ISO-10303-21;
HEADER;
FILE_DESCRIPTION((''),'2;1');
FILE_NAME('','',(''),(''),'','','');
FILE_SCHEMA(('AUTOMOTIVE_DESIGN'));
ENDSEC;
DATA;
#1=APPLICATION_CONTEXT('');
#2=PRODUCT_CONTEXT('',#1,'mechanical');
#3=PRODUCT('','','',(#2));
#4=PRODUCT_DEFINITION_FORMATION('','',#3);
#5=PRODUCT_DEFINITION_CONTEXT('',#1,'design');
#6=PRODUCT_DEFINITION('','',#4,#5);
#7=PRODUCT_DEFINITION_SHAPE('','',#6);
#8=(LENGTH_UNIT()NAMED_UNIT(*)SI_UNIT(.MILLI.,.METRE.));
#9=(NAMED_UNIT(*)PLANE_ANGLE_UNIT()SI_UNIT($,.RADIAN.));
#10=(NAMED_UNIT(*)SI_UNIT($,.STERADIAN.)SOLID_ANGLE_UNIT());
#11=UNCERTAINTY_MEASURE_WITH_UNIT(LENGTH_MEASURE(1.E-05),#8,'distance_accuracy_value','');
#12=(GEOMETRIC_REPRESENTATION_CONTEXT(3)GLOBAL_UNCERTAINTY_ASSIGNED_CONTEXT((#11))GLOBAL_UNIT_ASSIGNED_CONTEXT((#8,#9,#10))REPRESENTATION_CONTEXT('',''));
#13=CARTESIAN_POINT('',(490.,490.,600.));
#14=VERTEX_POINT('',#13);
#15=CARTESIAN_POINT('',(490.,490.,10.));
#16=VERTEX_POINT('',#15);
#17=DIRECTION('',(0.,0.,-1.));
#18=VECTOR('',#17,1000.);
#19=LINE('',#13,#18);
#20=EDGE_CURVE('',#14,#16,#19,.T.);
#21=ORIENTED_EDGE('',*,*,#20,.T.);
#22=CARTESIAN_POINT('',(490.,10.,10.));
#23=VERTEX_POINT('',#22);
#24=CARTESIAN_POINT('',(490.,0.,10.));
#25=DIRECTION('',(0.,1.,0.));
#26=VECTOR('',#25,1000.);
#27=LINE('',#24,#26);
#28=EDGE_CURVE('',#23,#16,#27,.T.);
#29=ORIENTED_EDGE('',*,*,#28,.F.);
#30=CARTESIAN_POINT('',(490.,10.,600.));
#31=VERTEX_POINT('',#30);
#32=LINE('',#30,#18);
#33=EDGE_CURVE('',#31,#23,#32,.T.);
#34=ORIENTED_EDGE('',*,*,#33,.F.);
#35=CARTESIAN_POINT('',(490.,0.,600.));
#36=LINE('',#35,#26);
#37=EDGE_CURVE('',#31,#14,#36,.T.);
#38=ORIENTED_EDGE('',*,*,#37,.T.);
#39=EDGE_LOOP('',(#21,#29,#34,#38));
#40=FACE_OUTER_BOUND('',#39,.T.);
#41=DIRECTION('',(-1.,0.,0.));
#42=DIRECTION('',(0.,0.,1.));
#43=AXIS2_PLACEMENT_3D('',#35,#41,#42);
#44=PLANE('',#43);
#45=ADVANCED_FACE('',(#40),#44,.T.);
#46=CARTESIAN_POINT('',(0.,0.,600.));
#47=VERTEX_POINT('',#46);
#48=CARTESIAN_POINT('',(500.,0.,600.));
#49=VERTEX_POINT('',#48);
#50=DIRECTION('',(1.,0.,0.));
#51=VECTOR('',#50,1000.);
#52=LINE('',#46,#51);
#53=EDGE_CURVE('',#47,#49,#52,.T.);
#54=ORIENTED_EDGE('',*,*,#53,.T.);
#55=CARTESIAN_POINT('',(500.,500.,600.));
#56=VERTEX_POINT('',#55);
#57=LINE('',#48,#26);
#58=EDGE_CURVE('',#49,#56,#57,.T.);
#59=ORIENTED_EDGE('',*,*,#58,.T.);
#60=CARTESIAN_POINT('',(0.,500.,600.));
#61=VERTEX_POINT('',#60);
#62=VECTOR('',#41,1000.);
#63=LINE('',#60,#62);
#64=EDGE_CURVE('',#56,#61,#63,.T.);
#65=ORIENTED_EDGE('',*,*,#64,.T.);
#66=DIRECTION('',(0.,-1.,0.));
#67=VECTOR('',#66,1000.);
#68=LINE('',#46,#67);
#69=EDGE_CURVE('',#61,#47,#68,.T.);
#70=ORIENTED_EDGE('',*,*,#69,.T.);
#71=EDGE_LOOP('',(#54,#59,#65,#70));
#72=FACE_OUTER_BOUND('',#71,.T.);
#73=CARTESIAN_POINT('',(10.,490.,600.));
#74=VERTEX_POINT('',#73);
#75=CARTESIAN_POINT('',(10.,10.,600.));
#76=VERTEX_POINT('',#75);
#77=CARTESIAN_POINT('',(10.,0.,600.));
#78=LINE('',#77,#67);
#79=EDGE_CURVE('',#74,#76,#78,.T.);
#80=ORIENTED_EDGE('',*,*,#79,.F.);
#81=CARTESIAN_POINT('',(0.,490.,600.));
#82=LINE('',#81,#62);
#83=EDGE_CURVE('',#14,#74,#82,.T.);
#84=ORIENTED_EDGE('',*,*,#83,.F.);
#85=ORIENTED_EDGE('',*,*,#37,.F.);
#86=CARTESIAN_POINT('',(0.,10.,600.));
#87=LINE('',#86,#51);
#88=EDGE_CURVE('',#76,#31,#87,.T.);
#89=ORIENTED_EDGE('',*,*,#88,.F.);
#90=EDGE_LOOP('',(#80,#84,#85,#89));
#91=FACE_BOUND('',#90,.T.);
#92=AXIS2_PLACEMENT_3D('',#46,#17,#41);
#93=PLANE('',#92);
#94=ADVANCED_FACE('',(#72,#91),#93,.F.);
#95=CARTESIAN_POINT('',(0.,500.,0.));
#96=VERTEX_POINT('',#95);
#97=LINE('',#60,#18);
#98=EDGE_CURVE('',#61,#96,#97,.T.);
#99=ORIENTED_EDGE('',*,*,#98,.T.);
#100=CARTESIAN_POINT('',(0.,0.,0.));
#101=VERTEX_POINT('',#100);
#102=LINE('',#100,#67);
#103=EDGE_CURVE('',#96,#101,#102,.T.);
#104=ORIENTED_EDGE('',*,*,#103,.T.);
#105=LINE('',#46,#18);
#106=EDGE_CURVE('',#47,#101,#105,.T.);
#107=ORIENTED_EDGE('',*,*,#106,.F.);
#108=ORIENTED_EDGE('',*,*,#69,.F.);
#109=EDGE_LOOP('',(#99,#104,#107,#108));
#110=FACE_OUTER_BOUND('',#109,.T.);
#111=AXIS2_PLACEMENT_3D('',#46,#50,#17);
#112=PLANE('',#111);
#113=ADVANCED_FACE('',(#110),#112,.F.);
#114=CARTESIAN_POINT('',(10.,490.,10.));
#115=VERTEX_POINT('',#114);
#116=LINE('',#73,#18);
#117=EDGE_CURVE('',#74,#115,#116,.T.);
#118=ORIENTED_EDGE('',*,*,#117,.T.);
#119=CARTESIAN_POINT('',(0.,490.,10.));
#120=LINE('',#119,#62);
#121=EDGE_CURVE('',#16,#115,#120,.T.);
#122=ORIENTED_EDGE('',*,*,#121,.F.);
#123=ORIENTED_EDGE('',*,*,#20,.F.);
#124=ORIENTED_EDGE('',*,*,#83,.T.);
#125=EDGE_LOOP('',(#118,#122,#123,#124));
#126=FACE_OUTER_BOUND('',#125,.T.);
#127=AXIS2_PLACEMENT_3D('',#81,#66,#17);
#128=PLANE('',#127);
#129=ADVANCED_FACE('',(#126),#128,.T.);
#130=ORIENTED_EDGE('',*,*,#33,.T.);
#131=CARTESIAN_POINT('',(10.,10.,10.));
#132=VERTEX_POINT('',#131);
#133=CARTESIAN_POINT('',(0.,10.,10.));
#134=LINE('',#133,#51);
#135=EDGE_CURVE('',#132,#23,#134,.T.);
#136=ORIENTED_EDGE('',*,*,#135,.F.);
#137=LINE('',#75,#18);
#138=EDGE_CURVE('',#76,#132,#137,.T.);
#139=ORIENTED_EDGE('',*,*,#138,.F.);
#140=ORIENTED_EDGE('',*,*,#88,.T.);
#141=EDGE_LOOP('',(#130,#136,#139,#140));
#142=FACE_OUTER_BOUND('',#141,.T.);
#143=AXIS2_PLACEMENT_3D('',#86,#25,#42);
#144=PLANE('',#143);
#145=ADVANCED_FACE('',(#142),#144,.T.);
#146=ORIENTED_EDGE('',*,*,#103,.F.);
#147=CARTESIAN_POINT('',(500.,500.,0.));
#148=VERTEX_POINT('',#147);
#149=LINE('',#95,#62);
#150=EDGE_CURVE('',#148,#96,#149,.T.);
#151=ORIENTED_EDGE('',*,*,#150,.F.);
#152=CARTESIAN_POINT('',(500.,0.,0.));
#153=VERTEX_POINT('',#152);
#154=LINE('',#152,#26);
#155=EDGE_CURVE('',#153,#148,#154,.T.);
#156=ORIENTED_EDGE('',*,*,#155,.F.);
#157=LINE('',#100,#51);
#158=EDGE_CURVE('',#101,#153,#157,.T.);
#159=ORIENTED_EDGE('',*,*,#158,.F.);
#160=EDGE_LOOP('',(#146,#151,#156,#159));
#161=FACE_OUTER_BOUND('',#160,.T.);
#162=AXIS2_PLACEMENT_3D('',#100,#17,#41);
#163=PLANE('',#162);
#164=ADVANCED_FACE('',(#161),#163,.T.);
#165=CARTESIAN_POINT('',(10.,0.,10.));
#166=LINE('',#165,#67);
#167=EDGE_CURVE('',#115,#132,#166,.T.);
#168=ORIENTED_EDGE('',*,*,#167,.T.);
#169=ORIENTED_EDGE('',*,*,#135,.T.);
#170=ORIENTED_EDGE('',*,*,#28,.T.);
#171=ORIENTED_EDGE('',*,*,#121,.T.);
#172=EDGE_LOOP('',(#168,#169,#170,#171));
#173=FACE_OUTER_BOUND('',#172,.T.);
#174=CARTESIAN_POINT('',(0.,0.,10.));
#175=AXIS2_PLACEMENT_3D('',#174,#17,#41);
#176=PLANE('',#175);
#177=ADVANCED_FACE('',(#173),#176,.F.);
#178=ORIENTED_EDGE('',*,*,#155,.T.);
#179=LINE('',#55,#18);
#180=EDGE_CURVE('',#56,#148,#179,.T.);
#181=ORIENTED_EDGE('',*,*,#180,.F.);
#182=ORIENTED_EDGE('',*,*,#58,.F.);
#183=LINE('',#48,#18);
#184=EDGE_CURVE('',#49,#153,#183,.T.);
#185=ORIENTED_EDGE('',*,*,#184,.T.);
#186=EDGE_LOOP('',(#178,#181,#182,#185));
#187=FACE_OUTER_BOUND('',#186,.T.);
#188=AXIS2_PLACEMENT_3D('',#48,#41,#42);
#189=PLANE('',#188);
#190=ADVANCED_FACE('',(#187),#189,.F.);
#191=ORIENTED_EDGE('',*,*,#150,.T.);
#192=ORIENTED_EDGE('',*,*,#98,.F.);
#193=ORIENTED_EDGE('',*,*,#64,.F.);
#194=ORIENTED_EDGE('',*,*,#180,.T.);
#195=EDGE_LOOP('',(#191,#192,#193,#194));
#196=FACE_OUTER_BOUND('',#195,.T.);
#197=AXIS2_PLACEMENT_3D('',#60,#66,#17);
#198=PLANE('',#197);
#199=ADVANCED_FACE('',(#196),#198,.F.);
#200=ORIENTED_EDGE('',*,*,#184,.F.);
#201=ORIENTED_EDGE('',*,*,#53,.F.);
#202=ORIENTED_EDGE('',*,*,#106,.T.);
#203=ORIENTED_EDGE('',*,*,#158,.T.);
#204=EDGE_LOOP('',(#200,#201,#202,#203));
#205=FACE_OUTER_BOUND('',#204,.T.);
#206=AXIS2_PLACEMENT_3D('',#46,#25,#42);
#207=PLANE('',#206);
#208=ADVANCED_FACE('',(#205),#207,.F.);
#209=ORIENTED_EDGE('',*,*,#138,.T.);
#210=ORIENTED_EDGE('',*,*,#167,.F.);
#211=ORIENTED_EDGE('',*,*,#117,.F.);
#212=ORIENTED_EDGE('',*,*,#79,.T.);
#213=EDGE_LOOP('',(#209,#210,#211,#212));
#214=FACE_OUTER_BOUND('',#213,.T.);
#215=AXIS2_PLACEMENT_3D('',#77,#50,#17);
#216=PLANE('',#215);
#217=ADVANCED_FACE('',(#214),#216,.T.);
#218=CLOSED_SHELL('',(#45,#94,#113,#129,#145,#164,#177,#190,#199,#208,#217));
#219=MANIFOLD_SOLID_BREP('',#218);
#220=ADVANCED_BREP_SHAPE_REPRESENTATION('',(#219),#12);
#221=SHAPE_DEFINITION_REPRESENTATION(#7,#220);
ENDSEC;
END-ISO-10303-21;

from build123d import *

# Parameters (mm, degrees)
SKETCH1_W           = 500
SKETCH1_H           = 500
BOSS_EXTRUDE1_DEPTH = 600
SHELL1_T            = -10


with BuildPart() as part:
    # Sketch1 → Boss-Extrude1 (new body)
    with BuildSketch(Plane.XY):
        with Locations((250, 250)):
            Rectangle(SKETCH1_W, SKETCH1_H)
    extrude(amount=BOSS_EXTRUDE1_DEPTH)

    # Shell1
    shell1_openings = [part.faces().sort_by_distance(p)[0] for p in [
        (250, 250, 600),
    ]]
    offset(amount=SHELL1_T, openings=shell1_openings, kind=Kind.INTERSECTION)


solid = part.part
